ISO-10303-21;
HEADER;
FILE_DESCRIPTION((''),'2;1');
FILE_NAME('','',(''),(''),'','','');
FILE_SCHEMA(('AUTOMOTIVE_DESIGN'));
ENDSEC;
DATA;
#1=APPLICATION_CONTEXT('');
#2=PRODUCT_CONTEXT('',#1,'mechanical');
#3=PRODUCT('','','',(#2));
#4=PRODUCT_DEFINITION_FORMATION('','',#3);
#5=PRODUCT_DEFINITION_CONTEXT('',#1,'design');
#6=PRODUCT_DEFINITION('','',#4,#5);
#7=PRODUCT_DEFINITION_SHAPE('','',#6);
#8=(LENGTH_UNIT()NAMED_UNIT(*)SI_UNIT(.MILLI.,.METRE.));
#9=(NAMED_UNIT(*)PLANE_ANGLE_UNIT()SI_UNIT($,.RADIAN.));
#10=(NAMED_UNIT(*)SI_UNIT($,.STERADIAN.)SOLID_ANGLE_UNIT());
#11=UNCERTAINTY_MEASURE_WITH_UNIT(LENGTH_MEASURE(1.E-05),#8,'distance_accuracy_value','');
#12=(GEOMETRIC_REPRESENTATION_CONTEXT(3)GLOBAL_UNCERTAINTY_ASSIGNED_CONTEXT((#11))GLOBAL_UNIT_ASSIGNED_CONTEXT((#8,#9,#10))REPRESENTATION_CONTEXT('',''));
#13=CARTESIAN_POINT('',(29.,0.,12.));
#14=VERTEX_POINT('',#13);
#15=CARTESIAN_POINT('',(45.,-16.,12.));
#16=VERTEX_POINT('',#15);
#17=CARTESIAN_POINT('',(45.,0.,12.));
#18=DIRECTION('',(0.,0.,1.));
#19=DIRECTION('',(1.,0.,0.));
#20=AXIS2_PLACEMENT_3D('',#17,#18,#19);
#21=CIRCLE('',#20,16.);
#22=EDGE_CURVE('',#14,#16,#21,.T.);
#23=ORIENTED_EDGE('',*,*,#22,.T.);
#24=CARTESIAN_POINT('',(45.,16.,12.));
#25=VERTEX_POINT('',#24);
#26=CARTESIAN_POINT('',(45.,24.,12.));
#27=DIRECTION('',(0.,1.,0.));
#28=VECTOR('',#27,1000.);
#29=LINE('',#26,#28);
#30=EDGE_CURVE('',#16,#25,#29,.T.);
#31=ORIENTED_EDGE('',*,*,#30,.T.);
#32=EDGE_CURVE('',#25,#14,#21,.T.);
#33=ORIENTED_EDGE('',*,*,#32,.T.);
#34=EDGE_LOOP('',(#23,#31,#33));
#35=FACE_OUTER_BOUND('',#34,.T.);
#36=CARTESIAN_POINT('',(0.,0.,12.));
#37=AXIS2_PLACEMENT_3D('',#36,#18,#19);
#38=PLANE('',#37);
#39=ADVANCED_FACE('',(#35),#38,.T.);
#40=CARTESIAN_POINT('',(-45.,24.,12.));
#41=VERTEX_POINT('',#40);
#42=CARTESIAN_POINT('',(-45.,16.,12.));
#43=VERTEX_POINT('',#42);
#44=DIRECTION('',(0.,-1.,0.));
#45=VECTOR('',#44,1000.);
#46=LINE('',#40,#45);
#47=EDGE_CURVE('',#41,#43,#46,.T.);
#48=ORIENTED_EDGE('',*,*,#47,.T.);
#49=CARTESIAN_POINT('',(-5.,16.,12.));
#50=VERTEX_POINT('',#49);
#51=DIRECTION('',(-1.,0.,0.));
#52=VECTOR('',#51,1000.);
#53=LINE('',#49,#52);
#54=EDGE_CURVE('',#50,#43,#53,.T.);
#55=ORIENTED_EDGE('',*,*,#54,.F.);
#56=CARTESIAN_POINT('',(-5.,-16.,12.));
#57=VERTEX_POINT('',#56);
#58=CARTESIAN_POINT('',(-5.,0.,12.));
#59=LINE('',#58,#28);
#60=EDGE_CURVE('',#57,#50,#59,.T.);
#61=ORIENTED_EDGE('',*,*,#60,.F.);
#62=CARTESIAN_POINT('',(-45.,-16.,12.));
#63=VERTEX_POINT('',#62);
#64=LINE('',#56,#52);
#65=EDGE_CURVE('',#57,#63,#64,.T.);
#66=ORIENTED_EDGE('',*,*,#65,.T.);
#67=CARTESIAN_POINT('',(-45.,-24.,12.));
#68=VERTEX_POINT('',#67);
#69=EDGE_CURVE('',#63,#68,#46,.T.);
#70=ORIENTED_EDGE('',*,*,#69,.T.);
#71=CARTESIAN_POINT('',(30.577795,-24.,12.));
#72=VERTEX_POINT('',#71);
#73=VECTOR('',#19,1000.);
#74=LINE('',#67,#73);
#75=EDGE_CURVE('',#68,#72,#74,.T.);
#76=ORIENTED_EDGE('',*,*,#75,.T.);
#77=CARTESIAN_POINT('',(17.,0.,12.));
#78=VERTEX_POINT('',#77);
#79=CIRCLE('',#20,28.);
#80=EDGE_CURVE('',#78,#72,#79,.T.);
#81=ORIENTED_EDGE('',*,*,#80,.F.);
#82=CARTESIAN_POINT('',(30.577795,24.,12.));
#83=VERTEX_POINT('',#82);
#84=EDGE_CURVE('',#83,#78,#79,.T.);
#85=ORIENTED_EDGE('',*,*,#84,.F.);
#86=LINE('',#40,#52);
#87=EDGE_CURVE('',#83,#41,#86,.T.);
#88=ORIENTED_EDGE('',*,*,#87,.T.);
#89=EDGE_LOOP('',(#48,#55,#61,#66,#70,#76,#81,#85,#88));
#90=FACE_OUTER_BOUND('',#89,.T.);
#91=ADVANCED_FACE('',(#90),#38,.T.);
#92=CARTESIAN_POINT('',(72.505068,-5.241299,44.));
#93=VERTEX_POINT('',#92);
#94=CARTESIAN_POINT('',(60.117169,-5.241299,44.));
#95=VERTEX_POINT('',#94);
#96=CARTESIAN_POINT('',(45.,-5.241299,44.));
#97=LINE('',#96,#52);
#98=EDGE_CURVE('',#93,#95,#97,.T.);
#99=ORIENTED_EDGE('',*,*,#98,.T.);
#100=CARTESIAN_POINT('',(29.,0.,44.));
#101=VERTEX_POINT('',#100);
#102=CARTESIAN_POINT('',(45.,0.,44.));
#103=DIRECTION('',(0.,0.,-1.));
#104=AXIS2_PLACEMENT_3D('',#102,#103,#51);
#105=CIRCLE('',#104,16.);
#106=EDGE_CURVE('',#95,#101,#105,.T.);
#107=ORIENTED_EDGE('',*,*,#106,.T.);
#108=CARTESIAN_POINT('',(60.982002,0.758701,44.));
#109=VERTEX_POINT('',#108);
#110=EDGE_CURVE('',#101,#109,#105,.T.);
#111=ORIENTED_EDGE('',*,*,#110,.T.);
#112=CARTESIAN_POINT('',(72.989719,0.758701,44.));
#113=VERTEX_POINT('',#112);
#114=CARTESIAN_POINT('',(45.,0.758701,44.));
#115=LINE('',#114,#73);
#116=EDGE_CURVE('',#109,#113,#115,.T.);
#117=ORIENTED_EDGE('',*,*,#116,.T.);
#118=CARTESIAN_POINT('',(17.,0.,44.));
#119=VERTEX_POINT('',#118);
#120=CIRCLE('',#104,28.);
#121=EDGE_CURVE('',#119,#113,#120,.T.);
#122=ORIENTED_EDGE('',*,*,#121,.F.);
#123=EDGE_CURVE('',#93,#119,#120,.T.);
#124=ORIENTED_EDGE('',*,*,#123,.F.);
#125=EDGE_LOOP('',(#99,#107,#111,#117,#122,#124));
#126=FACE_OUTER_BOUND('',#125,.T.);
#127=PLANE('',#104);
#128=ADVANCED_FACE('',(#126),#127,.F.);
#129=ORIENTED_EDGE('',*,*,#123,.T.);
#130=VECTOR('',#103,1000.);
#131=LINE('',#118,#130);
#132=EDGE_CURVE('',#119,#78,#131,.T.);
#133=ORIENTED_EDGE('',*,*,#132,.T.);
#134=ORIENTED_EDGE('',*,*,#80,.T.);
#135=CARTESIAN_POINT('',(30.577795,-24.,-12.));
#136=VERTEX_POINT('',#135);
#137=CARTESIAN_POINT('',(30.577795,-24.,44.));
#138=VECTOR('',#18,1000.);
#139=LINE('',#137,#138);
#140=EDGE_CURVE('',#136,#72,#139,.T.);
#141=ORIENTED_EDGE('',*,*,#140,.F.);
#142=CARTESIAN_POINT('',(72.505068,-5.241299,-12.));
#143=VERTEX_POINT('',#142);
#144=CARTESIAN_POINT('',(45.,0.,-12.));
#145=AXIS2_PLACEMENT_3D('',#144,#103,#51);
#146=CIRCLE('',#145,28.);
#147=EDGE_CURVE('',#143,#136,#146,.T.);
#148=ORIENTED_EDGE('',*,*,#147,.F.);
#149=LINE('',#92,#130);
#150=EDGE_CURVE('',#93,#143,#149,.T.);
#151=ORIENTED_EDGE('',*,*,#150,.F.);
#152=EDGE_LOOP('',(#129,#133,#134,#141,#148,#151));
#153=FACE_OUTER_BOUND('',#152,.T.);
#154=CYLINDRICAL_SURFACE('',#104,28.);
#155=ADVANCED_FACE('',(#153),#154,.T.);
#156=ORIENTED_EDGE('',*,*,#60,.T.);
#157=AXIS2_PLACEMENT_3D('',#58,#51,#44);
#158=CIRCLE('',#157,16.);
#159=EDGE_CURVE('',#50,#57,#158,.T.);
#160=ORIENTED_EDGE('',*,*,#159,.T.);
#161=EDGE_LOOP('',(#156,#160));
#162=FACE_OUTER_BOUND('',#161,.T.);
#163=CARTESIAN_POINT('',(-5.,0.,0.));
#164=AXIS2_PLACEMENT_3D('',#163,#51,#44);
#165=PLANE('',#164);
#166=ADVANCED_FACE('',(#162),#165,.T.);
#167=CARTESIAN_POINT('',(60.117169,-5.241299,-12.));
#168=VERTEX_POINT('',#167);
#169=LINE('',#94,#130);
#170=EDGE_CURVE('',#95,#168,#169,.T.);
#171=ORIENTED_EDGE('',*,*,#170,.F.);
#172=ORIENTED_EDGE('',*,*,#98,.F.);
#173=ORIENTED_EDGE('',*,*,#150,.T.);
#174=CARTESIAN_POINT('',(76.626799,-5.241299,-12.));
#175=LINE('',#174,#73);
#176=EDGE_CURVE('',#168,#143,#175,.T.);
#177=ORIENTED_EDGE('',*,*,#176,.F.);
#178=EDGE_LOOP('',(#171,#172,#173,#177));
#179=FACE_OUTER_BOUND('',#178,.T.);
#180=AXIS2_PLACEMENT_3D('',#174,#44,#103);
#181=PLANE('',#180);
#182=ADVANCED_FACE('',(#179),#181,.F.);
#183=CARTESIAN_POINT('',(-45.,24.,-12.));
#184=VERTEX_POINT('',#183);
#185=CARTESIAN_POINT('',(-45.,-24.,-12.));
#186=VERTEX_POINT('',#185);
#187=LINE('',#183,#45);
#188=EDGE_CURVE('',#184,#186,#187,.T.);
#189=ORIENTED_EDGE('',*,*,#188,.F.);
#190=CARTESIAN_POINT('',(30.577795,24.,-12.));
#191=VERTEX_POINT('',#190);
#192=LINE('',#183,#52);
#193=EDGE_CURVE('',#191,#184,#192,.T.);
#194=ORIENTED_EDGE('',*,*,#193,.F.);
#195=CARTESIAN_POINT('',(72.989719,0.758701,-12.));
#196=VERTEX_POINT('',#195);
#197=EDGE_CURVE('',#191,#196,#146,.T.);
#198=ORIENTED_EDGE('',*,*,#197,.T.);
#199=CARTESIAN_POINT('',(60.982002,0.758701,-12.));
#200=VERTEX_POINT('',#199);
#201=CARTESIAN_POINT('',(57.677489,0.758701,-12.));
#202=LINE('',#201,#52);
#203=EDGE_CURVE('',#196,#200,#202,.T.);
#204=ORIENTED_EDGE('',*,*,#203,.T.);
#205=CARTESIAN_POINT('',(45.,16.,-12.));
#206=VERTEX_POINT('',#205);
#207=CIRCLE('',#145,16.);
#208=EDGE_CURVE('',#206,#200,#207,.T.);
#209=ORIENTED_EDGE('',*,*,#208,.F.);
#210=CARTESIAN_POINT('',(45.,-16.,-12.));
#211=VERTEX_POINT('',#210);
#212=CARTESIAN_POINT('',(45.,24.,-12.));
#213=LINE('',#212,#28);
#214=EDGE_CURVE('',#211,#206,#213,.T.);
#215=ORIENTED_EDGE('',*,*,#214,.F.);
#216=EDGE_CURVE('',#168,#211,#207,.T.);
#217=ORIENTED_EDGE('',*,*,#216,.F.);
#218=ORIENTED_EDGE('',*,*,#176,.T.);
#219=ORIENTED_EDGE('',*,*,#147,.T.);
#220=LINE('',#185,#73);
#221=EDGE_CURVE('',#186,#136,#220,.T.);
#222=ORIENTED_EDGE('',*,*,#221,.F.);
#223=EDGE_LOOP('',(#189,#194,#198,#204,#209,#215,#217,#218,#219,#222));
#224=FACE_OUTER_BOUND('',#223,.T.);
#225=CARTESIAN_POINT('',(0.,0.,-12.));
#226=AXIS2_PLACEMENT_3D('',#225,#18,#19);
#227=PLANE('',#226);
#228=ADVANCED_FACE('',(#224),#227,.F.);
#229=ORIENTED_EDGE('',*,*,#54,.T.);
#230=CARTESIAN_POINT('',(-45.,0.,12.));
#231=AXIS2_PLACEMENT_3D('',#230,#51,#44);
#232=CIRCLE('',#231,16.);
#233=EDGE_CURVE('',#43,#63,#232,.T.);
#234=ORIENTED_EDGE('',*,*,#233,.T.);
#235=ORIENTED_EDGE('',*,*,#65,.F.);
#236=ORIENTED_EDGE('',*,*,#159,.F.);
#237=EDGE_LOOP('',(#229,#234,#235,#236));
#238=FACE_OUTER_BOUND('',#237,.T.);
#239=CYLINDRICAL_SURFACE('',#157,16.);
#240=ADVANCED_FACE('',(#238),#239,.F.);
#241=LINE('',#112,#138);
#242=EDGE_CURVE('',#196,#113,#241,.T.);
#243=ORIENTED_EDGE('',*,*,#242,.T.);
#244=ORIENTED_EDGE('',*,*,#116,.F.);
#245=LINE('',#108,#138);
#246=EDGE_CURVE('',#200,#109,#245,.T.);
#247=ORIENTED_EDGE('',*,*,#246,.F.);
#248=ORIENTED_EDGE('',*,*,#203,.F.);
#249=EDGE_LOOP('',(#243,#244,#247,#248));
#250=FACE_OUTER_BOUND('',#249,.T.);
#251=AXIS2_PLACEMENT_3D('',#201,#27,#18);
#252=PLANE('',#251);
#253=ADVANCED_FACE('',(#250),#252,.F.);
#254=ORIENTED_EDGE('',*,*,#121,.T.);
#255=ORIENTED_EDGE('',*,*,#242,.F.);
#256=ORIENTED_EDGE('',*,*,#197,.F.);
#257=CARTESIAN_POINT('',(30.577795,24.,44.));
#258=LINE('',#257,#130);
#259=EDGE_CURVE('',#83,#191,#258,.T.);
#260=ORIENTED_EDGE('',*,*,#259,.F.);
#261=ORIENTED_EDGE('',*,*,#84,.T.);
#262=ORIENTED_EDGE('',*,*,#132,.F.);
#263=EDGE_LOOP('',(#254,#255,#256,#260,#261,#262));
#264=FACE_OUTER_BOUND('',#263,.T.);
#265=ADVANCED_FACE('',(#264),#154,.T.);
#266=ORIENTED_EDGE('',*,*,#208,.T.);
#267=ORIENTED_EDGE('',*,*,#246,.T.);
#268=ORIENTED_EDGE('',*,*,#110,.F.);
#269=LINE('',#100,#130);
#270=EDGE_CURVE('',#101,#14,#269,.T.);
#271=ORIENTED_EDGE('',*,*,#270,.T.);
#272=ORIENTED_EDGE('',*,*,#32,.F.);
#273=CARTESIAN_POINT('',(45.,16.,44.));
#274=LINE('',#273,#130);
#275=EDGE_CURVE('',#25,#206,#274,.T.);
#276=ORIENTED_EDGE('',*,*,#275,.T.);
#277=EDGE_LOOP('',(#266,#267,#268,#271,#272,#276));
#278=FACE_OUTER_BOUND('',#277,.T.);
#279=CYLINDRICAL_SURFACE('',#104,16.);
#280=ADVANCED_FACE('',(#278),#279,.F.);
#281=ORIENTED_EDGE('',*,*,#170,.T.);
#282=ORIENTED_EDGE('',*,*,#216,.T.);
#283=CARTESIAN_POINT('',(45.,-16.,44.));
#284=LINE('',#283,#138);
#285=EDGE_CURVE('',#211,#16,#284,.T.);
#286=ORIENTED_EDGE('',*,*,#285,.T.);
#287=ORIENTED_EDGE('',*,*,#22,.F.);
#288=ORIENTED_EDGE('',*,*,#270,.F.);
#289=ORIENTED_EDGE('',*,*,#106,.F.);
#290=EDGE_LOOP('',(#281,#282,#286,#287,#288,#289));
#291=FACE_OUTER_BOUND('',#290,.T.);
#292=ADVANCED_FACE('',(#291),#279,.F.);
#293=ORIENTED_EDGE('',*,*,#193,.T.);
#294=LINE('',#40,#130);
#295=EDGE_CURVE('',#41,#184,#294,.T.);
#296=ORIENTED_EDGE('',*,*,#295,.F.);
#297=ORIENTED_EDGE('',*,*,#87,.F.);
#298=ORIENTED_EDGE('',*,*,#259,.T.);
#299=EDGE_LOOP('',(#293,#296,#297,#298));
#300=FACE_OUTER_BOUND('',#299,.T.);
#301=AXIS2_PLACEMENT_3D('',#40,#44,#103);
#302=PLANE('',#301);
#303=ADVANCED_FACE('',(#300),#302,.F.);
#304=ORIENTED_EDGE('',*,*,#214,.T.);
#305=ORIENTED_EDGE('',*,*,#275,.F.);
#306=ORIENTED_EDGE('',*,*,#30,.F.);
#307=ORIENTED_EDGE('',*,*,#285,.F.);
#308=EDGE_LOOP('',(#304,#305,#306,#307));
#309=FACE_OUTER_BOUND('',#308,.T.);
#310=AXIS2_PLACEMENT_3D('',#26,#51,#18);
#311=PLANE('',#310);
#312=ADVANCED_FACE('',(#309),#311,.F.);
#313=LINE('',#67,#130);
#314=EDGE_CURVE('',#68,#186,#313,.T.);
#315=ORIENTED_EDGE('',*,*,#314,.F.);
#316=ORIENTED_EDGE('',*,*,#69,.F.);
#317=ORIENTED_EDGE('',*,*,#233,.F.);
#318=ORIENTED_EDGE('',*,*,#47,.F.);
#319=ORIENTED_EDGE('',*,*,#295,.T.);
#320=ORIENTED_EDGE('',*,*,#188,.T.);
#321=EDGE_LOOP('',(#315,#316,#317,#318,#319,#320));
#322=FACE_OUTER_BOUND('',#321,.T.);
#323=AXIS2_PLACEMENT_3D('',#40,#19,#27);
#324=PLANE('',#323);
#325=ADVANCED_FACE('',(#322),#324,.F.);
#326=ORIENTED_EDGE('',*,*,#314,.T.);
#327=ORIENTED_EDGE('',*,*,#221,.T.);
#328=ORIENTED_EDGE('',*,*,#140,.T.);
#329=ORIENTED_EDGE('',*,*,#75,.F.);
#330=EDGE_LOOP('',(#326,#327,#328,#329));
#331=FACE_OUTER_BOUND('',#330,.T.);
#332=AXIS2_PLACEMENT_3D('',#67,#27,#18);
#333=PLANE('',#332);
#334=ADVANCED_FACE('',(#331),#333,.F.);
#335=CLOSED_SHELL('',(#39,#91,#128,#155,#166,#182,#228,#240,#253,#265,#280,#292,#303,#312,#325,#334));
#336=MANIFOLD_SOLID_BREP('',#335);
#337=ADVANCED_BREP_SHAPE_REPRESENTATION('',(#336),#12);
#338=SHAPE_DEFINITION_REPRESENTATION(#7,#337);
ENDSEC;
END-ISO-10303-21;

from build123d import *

# Parameters (mm, degrees)
BASE_BLOCK_SKETCH_W           = 90
BASE_BLOCK_SKETCH_H           = 48
BASE_BLOCK_DEPTH              = 12
CRADLE_CUT_DEPTH              = 40
CLAMP_BOSS_SKETCH_R           = 28
CLAMP_BOSS_SKETCH_R_2         = 16
CLAMP_BOSS_56_DEPTH           = 56
BORE_AND_SPLIT_SLOT_CUT_DEPTH = 56


with BuildPart() as part:
    # Base Block Sketch → Base Block (new, symmetric)
    with BuildSketch(Plane.XY):
        Rectangle(BASE_BLOCK_SKETCH_W, BASE_BLOCK_SKETCH_H)
    extrude(amount=BASE_BLOCK_DEPTH, both=True)

    # Cradle Cut Sketch → Cradle Cut (cut)
    with BuildSketch(Plane.ZY.offset(45)):
        with BuildLine():
            Line((12, -16), (12, 16))
            ThreePointArc((12, 16), (-4, 0), (12, -16))
        make_face()
    extrude(amount=-CRADLE_CUT_DEPTH, mode=Mode.SUBTRACT)

    # Clamp Boss Sketch → Clamp Boss Ø56 (add)
    with BuildSketch(Plane(origin=(0, 0, -12), x_dir=(-1, 0, 0), z_dir=(0, 0, -1))):
        with Locations((-45, 0)):
            Circle(CLAMP_BOSS_SKETCH_R)
        with Locations((-45, 0)):
            Circle(CLAMP_BOSS_SKETCH_R_2, mode=Mode.SUBTRACT)
    extrude(amount=-CLAMP_BOSS_56_DEPTH)

    # Bore and Split Slot Sketch → Bore and Split Slot Cut (cut)
    with BuildSketch(Plane.XY.offset(44)):
        Polygon((57.677488521, -2.241298623), (57.677488521, 0.758701377), (76.626798925, 0.758701377), (76.626798925, -5.241298623), (57.677488521, -5.241298623), align=None)
    extrude(amount=-BORE_AND_SPLIT_SLOT_CUT_DEPTH, mode=Mode.SUBTRACT)


solid = part.part
